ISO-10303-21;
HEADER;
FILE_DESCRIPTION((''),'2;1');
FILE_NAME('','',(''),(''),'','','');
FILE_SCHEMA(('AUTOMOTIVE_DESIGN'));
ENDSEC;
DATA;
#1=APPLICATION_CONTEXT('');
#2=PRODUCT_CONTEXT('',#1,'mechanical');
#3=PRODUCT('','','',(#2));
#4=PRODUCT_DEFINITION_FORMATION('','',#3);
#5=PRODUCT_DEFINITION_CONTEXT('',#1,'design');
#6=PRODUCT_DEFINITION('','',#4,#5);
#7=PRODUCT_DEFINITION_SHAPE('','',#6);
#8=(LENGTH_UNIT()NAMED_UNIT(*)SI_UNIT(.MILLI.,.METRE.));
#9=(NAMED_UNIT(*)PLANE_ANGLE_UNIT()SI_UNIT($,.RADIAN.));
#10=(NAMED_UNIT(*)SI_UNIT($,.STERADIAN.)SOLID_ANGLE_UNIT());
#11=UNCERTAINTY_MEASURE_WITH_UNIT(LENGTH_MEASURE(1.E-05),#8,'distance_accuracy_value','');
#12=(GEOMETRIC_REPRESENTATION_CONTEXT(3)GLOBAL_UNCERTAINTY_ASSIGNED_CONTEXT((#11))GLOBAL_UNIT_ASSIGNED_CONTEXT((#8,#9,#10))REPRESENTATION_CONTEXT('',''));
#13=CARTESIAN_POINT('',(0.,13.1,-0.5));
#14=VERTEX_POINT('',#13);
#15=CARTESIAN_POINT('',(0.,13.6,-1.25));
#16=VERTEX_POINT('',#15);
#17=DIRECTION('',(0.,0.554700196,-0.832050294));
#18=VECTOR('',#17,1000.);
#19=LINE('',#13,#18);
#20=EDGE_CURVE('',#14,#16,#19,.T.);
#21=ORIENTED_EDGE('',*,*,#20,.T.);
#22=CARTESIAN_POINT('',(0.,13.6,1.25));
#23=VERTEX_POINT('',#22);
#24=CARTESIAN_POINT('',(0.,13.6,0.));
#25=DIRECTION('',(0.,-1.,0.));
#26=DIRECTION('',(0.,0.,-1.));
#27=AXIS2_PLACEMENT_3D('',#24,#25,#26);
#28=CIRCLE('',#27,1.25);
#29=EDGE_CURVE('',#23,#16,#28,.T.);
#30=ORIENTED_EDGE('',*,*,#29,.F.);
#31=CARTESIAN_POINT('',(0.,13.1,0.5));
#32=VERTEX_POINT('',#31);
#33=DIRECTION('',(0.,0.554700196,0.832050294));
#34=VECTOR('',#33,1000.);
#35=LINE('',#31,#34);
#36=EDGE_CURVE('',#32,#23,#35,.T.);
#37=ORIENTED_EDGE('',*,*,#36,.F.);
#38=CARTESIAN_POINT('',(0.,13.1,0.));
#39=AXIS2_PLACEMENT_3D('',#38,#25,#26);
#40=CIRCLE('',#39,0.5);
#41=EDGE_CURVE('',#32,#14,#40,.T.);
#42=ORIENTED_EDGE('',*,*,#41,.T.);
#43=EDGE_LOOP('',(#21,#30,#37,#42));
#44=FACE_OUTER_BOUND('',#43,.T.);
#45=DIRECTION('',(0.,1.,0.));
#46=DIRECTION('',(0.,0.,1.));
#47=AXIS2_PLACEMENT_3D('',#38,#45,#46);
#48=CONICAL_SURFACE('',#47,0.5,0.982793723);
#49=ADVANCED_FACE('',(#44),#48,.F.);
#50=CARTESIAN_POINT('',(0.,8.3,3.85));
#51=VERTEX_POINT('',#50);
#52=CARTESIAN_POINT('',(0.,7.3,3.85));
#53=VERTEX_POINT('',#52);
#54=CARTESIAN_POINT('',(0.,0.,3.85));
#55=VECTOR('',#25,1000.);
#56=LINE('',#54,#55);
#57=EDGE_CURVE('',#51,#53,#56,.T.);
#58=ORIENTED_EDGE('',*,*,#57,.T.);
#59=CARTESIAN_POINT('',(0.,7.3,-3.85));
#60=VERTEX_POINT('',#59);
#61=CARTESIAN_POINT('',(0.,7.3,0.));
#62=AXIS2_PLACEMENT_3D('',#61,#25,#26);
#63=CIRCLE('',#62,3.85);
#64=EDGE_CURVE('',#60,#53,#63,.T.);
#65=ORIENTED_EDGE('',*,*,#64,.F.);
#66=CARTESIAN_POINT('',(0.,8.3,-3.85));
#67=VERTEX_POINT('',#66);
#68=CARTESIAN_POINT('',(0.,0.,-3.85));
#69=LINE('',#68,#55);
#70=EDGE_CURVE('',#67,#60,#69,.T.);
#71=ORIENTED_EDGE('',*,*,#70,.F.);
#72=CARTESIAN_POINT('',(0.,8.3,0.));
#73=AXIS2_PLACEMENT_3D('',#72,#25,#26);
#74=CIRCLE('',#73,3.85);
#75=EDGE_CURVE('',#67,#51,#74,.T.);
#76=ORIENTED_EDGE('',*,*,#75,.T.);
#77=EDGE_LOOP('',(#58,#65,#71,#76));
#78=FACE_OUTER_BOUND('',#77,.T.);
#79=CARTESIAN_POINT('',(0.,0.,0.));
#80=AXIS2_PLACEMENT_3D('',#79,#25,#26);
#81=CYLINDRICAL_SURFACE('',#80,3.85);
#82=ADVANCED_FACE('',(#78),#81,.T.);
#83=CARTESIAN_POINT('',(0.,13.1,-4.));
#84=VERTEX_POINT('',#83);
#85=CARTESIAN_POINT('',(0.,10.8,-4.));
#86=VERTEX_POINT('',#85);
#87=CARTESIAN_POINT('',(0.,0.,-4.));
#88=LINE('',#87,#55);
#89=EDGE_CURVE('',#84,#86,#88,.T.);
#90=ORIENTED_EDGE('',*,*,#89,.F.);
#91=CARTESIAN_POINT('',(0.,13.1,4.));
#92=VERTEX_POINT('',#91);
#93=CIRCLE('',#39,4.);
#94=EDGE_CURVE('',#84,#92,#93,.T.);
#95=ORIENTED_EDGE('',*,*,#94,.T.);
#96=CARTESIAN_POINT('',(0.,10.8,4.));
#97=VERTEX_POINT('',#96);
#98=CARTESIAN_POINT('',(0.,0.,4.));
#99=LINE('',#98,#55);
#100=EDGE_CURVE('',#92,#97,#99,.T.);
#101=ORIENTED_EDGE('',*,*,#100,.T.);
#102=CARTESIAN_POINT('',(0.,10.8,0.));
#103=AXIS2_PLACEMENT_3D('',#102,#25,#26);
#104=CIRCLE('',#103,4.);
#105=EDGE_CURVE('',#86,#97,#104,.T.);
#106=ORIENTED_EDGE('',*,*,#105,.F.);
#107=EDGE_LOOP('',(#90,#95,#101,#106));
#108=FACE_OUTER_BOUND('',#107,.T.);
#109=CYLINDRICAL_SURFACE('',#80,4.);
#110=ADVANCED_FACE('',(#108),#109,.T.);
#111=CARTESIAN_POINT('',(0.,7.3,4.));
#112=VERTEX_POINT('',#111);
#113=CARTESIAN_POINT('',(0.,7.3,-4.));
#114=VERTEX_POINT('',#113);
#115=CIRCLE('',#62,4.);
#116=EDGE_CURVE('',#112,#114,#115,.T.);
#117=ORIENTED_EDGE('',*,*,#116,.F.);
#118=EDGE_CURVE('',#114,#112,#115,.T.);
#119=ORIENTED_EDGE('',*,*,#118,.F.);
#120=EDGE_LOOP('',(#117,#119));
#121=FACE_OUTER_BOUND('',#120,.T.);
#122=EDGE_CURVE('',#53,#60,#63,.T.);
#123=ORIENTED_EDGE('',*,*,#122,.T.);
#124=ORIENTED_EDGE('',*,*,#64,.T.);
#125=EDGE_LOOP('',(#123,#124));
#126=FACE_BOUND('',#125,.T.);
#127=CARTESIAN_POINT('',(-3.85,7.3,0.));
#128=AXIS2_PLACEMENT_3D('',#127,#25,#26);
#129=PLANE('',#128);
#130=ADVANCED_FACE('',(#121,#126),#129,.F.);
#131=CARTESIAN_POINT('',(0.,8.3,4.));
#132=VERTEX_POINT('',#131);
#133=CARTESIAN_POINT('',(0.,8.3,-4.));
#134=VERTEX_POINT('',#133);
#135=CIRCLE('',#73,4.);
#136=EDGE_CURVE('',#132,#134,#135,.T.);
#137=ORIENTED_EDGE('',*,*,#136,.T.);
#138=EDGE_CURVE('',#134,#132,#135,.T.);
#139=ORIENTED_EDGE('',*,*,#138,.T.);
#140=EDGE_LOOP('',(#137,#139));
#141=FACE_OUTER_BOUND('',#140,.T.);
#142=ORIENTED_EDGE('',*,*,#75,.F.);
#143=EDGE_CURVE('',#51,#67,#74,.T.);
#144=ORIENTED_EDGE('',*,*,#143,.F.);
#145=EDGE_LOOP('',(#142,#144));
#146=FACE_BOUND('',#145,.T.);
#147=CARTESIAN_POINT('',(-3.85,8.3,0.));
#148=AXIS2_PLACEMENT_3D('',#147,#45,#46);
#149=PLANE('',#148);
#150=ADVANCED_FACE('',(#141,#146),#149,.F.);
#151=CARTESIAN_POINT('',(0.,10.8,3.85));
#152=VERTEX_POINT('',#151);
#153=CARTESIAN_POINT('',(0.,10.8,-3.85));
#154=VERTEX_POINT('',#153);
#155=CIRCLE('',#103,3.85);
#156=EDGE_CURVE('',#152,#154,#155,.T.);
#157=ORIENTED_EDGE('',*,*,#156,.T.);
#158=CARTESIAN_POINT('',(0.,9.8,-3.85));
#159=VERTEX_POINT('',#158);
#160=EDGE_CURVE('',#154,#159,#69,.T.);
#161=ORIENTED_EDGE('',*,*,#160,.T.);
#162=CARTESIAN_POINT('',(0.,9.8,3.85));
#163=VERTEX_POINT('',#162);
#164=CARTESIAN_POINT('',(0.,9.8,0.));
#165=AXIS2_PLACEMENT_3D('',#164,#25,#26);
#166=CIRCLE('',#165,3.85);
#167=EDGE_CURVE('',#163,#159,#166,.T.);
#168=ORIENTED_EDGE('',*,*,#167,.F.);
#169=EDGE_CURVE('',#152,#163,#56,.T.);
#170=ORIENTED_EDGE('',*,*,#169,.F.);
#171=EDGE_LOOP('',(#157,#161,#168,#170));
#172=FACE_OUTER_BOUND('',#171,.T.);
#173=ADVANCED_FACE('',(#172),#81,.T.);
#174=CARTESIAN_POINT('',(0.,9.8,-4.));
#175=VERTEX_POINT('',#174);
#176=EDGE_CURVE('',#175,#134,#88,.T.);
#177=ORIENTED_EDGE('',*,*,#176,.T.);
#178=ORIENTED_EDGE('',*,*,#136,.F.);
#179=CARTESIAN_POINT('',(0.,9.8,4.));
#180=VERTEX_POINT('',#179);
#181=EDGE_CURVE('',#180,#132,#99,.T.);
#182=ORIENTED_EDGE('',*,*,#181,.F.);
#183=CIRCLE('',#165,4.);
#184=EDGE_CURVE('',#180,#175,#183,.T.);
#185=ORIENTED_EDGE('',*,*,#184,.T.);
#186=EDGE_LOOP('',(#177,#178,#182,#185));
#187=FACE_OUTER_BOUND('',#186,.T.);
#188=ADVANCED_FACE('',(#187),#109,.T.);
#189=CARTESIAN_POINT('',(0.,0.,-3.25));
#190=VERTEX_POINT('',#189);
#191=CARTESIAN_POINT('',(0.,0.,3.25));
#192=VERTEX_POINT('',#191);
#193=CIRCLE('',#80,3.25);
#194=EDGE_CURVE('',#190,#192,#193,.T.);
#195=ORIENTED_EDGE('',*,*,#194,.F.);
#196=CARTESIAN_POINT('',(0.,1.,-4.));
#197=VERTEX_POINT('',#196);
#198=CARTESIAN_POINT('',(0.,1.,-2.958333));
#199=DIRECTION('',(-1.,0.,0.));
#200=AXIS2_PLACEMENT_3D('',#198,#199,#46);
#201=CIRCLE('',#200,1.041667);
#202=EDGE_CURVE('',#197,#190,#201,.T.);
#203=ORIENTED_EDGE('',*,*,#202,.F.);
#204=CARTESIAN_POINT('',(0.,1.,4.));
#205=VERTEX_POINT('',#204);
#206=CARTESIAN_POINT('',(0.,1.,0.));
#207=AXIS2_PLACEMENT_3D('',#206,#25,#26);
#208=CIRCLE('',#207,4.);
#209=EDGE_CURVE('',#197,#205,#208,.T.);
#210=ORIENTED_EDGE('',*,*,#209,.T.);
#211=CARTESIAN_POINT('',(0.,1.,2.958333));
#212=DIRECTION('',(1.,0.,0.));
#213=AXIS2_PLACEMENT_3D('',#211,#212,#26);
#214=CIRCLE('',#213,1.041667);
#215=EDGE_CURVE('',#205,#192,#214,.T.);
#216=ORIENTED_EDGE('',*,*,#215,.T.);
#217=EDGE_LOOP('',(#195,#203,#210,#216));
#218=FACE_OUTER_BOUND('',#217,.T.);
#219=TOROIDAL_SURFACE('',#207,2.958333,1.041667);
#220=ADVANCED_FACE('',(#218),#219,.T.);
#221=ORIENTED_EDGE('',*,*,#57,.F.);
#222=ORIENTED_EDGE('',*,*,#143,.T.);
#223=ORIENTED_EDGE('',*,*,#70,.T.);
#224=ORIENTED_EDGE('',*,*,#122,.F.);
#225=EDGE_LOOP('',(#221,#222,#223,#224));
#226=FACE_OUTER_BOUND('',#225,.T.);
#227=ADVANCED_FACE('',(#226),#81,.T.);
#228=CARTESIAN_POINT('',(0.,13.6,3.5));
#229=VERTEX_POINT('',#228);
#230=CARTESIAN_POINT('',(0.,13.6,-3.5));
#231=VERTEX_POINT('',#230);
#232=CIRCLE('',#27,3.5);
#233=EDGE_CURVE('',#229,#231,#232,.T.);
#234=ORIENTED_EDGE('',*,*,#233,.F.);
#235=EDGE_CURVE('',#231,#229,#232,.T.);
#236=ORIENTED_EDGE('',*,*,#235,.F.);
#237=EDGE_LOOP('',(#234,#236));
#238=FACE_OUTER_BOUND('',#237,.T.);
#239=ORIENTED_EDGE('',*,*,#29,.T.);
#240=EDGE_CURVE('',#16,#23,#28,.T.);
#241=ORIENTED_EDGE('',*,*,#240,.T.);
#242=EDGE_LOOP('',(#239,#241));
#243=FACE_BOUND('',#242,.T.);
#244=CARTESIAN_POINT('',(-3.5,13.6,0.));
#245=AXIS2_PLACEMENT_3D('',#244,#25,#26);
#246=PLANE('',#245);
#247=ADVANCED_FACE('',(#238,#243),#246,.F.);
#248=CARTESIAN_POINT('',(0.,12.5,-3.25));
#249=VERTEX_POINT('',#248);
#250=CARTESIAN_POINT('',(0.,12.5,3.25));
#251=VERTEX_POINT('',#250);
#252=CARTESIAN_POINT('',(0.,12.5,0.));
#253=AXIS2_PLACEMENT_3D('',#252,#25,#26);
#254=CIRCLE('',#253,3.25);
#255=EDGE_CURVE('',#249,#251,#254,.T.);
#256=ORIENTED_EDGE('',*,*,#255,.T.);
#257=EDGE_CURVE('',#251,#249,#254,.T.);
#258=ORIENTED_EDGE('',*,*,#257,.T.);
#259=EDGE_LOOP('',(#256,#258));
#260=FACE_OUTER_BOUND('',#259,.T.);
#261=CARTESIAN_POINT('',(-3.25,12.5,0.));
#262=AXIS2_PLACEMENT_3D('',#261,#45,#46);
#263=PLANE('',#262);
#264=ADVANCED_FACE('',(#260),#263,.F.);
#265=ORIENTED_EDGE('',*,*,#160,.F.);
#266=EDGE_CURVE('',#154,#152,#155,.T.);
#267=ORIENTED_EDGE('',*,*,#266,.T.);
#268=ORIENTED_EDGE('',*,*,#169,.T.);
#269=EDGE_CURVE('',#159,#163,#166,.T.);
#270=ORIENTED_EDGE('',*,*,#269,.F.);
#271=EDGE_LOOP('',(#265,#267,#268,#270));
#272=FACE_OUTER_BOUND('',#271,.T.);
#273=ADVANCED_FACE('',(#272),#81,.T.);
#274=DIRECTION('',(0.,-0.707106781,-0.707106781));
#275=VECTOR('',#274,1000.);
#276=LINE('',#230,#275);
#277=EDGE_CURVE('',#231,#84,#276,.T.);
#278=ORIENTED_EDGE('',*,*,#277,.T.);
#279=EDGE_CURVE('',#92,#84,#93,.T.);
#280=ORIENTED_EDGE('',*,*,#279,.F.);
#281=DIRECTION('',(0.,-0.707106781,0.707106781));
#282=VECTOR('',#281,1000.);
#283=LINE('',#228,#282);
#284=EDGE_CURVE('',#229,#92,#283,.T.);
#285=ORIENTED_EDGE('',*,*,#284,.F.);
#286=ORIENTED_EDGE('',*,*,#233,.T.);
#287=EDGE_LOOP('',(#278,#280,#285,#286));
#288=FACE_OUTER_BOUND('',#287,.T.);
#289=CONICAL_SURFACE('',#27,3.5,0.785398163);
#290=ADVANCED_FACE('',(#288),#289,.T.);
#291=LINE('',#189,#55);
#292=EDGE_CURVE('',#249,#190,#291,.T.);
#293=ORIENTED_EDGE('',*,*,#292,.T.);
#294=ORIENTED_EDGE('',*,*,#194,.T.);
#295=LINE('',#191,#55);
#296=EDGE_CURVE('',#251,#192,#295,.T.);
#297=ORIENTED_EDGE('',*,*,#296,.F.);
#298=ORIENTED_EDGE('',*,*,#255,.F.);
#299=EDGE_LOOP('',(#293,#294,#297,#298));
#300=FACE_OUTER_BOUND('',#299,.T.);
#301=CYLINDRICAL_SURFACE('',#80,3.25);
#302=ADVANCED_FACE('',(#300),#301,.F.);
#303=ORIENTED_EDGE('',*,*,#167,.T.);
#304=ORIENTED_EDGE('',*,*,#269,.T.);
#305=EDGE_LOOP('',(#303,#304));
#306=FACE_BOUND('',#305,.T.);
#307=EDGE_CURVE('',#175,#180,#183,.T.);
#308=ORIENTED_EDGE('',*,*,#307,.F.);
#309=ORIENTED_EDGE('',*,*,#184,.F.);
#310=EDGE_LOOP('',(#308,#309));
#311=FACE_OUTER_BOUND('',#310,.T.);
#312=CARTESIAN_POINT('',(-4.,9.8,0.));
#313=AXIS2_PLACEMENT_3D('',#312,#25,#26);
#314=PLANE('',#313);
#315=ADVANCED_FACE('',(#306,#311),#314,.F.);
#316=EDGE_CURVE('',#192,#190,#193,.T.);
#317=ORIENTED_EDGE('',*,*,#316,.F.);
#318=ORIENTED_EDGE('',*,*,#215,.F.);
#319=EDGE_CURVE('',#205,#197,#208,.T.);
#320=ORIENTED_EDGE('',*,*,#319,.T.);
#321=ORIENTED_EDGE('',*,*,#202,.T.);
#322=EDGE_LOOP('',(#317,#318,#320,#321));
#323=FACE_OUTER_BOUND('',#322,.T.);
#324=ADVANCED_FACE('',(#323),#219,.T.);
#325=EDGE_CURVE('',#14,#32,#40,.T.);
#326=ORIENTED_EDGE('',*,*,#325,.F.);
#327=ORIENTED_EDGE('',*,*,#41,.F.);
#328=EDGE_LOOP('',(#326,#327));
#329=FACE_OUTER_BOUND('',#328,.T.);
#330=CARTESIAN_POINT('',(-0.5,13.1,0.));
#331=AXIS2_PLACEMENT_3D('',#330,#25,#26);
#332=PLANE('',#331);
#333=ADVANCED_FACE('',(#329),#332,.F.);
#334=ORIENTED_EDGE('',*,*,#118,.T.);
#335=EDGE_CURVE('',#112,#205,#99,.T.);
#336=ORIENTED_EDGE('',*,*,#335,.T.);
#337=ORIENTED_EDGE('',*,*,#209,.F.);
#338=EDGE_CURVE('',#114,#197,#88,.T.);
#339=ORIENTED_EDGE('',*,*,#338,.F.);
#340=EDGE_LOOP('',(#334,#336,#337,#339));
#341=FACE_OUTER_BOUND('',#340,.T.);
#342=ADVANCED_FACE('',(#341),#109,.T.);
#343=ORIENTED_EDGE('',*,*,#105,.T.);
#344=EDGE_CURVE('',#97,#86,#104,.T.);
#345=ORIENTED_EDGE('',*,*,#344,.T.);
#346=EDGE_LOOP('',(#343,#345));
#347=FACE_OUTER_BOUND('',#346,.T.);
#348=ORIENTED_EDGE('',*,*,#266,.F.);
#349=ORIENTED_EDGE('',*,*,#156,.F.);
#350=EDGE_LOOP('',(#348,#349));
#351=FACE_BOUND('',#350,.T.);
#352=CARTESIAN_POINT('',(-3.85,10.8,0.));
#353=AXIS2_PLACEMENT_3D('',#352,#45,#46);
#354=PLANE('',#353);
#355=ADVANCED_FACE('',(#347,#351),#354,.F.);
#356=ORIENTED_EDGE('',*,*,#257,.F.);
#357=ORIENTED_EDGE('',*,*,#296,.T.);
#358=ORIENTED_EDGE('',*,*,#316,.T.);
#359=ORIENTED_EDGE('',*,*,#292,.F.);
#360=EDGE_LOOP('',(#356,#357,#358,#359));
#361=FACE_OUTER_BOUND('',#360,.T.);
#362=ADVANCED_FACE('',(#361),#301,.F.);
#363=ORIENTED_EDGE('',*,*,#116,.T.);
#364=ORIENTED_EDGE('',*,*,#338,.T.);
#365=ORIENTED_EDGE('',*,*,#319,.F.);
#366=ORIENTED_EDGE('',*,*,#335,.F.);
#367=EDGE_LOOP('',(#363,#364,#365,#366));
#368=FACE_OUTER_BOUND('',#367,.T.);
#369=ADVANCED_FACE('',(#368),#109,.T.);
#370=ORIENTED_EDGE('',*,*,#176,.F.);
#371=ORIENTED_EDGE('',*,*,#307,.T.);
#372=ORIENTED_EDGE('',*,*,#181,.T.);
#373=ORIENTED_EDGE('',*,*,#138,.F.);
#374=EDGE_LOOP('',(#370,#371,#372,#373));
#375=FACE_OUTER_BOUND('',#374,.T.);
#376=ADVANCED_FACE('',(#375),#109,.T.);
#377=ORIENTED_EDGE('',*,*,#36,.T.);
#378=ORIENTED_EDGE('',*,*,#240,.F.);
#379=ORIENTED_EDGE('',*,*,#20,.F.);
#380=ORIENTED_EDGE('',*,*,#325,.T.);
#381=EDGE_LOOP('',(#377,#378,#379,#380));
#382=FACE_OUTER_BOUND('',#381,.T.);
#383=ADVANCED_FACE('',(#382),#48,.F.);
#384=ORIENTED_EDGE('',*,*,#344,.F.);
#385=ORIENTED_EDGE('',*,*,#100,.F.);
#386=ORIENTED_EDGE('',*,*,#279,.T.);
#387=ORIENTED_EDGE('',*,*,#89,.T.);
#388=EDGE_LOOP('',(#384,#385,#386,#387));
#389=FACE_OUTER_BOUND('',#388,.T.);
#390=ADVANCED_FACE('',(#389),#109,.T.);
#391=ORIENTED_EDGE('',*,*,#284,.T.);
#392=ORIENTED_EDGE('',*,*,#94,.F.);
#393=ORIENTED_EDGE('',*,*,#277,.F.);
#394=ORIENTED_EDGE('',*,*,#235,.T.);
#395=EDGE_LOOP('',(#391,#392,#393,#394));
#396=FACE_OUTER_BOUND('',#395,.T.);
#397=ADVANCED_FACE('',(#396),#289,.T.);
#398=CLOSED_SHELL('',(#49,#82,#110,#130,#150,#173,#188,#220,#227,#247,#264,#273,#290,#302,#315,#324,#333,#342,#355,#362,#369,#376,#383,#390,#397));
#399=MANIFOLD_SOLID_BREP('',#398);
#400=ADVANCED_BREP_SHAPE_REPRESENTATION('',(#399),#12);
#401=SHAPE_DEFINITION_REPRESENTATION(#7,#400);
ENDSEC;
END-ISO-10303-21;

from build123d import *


with BuildPart() as part:
    # 草图1 → 旋转1 (revolve)
    with BuildSketch(Plane.XY, mode=Mode.PRIVATE) as revolve_1_sk:
        with BuildLine():
            Line((-3.25, 0), (-3.25, 12.5))
            Line((-3.25, 12.5), (0, 12.5))
            Line((0, 12.5), (0, 13.1))
            Line((0, 13.1), (-0.5, 13.1))
            Line((-0.5, 13.1), (-1.25, 13.6))
            Line((-1.25, 13.6), (-3.5, 13.6))
            Line((-3.5, 13.6), (-4, 13.1))
            Line((-4, 13.1), (-4, 10.8))
            Line((-4, 10.8), (-3.85, 10.8))
            Line((-3.85, 10.8), (-3.85, 9.8))
            Line((-3.85, 9.8), (-4, 9.8))
            Line((-4, 9.8), (-4, 8.3))
            Line((-4, 8.3), (-3.85, 8.3))
            Line((-3.85, 8.3), (-3.85, 7.3))
            Line((-3.85, 7.3), (-4, 7.3))
            Line((-4, 7.3), (-4, 1))
            ThreePointArc((-4, 1), (-3.791666667, 0.375), (-3.25, 0))
        make_face()
    revolve(revolve_1_sk.sketch.rotate(Axis((0, 0, 0), (0, 1, 0)), 270), axis=Axis((0, 0, 0), (0, 1, 0)))


solid = part.part
